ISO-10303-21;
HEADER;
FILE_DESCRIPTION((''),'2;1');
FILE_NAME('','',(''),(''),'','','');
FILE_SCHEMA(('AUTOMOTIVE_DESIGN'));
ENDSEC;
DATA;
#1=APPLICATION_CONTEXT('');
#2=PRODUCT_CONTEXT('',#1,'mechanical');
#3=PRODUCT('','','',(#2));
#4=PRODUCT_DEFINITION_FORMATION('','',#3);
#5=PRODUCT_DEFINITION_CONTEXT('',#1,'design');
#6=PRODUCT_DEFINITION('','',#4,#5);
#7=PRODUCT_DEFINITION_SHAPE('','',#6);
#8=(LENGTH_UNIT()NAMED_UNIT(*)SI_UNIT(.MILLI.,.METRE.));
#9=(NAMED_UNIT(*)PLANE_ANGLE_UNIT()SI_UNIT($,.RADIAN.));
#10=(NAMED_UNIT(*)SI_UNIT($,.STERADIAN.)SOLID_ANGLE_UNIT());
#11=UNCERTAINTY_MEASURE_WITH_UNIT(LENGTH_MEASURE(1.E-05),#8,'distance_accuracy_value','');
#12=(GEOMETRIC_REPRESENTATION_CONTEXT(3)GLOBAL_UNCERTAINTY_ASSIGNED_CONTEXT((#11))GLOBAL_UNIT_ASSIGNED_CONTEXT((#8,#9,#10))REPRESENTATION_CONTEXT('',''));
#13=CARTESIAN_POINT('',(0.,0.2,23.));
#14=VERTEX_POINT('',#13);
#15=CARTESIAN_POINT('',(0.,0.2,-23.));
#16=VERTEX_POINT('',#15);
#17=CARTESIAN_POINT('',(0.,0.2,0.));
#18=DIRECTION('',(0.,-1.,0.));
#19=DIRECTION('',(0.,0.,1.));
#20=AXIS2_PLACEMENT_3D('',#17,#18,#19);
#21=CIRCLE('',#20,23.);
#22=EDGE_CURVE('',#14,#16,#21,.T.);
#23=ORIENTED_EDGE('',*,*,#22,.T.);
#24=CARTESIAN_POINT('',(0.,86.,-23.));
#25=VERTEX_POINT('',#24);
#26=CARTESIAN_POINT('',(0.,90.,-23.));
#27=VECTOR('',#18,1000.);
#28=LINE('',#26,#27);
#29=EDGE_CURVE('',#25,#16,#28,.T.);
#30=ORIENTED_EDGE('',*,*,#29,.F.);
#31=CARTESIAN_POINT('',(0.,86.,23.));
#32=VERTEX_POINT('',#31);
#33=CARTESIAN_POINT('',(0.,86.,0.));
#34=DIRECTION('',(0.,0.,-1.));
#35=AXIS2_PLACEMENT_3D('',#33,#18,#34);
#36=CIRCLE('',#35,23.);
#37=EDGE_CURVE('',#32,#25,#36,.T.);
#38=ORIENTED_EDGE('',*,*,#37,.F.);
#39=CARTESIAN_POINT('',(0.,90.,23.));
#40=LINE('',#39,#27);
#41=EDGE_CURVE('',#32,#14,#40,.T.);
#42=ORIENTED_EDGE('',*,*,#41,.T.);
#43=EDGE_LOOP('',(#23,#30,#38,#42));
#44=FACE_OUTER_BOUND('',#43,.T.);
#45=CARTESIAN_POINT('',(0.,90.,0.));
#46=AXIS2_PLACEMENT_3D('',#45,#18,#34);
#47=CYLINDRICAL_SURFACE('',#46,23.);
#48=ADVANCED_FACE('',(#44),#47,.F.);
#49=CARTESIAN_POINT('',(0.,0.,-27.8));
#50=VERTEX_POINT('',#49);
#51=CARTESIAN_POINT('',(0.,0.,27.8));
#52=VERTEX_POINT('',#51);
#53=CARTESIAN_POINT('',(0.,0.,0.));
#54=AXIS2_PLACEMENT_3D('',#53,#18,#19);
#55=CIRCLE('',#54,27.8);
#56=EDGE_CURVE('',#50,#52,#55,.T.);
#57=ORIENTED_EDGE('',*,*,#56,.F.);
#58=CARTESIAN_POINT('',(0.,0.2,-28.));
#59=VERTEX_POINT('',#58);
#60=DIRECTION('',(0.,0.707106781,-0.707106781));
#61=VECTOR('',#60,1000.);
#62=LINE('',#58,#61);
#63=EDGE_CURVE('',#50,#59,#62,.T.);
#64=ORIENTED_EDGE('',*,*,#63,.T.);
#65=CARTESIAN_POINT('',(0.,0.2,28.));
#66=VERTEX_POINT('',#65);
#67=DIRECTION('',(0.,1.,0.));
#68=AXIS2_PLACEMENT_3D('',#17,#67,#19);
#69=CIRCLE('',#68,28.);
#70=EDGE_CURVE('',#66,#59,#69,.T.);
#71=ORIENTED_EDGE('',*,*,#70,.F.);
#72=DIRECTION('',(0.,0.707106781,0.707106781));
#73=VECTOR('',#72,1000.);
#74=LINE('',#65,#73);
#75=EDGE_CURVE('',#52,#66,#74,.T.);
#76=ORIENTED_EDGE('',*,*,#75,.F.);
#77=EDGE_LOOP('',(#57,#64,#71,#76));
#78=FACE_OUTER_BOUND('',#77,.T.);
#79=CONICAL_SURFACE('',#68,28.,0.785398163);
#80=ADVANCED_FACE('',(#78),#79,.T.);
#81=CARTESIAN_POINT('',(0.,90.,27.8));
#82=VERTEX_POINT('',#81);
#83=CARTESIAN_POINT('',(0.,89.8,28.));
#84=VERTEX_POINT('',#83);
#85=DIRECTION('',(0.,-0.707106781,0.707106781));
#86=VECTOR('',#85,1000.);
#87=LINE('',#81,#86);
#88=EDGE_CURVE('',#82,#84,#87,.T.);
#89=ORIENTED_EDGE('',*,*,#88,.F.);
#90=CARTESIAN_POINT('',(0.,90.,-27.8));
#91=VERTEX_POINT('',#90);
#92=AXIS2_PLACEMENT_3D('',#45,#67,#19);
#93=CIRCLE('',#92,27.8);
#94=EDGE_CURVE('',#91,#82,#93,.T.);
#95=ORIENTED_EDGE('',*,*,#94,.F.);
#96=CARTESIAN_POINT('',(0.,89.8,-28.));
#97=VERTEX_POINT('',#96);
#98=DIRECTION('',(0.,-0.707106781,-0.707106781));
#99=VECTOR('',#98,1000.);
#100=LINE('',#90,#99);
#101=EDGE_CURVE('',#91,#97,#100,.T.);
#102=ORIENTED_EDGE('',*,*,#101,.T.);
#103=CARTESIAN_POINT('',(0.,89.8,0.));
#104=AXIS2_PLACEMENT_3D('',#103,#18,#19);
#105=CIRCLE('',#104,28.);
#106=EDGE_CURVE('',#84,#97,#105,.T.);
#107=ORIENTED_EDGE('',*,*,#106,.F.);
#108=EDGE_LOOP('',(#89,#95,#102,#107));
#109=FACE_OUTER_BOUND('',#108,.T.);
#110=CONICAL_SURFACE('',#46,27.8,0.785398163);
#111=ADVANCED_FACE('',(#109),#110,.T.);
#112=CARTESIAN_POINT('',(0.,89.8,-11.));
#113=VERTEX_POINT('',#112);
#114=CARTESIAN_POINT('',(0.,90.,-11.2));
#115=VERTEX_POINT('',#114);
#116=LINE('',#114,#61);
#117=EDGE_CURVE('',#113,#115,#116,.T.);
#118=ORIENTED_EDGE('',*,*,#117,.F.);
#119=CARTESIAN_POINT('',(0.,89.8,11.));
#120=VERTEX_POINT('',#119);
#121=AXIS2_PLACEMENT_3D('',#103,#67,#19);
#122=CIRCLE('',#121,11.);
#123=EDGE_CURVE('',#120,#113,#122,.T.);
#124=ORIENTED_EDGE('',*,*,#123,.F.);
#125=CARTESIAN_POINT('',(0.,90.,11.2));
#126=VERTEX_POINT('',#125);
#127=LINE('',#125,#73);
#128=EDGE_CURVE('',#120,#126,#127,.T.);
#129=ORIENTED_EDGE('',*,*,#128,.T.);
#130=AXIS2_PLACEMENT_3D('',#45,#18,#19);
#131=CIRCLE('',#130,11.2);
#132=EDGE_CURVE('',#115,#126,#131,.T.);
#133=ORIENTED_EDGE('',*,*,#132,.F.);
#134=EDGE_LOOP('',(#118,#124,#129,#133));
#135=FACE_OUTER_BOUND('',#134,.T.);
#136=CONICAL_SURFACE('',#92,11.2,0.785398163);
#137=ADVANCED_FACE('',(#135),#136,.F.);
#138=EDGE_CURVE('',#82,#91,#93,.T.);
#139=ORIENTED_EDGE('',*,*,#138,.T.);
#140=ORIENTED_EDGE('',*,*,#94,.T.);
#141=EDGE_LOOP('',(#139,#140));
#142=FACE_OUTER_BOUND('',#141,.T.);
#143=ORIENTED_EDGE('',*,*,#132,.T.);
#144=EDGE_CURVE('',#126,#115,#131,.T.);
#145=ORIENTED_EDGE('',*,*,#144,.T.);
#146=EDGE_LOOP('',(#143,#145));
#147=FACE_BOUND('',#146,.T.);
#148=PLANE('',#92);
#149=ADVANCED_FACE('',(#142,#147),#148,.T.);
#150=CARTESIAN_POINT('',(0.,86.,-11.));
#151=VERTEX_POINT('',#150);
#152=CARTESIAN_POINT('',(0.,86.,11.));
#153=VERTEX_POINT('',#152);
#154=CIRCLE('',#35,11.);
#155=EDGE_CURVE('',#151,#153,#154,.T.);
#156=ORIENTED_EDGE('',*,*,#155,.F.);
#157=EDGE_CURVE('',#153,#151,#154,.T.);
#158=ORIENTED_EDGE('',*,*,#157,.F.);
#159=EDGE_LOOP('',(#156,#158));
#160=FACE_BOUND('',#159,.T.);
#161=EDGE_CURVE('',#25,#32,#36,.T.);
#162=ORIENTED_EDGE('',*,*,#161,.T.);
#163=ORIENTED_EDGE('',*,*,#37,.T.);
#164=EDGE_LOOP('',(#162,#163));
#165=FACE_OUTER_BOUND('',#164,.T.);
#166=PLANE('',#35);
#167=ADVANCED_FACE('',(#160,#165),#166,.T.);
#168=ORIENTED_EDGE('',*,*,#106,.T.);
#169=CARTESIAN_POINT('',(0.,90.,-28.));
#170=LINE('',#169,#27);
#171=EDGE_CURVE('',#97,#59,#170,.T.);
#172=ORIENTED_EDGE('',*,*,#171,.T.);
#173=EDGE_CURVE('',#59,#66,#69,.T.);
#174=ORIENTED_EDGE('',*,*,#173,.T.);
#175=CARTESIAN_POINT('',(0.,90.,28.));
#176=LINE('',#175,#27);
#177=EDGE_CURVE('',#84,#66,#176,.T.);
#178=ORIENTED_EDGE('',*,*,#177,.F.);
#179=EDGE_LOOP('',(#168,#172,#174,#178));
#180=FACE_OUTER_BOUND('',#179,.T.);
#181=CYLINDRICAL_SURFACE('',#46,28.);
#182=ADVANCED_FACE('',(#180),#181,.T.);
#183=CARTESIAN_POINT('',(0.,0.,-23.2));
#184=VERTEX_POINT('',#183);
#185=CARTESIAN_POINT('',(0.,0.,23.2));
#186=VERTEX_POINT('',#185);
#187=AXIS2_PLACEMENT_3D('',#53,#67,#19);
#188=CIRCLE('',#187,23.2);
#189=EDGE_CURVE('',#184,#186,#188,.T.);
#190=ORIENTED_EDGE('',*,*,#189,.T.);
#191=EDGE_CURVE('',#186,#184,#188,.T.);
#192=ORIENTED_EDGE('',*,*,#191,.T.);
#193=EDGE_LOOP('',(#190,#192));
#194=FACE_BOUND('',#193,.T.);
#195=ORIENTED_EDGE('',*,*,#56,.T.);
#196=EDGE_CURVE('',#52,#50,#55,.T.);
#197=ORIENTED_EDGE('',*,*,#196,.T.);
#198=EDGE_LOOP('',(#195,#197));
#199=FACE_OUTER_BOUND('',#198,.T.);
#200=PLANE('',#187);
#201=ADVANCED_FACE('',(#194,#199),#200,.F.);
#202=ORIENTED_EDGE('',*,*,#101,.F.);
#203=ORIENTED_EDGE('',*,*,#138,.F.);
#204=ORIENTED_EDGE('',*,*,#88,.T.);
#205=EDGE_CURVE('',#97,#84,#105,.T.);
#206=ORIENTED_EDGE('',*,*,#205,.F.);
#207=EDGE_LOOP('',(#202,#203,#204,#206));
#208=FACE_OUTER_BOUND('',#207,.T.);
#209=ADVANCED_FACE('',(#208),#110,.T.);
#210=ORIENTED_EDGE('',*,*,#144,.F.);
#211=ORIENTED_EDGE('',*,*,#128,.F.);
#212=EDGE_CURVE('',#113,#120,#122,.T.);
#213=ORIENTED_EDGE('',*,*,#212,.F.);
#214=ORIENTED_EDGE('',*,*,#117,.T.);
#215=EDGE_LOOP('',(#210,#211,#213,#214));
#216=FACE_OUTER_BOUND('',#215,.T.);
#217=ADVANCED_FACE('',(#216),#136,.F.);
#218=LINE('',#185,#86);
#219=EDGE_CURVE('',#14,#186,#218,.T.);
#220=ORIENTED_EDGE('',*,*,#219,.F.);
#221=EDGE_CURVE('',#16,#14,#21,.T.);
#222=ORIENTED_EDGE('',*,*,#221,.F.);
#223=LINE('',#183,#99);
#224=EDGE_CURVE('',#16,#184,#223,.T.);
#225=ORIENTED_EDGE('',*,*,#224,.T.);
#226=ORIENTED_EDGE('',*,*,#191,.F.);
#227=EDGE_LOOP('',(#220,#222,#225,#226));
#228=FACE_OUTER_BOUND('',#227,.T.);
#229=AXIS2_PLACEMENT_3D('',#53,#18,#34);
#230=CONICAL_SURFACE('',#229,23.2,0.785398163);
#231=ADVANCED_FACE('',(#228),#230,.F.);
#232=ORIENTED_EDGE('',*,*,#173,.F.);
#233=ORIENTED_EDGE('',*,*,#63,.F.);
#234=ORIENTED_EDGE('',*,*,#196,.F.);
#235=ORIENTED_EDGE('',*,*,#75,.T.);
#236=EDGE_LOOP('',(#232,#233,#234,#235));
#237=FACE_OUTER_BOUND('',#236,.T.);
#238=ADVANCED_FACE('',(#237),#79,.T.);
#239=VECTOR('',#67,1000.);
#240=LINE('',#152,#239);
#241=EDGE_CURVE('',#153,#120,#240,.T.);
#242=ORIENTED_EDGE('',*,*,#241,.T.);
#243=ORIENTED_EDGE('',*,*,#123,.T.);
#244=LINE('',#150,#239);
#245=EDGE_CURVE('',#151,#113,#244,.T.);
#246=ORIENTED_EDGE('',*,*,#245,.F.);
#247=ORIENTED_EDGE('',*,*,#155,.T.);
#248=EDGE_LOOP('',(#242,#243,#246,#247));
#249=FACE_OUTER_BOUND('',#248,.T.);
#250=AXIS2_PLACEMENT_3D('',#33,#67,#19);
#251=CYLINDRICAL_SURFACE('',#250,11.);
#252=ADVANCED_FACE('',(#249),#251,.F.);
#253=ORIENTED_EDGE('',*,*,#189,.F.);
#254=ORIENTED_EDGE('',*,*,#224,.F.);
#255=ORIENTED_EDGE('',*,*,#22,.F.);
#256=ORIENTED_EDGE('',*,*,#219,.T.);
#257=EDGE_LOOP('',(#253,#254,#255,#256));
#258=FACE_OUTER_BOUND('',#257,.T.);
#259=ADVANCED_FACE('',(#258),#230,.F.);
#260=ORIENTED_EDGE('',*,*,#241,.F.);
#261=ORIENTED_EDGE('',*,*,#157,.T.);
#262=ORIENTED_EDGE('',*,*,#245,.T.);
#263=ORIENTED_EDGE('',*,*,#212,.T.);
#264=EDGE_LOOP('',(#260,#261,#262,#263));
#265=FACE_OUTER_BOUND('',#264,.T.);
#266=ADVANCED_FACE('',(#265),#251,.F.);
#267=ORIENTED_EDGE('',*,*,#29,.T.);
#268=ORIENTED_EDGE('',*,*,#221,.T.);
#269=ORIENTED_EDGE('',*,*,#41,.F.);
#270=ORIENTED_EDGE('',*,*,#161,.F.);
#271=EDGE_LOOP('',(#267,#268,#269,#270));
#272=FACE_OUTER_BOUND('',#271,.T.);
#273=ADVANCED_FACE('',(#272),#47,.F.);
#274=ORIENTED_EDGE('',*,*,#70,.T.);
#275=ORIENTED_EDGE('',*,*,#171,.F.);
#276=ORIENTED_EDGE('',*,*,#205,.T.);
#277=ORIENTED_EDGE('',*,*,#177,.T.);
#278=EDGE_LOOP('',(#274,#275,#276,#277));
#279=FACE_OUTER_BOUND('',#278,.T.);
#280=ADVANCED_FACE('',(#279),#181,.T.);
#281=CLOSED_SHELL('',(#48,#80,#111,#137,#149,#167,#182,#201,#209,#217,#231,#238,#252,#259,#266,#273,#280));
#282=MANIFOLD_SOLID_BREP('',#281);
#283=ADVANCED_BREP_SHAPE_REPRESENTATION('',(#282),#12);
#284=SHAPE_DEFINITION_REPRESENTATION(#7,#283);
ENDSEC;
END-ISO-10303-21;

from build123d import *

# Parameters (mm, degrees)
SKETCH_3_R      = 28
SKETCH_3_R_2    = 23
EXTRUDE_1_DEPTH = 90
SKETCH_4_R      = 23.5
SKETCH_4_R_2    = 11
EXTRUDE_2_DEPTH = 4
CHAMFER_1_SIZE  = 0.2


with BuildPart() as part:
    # 草图3 → 凸台-拉伸1 (new body)
    with BuildSketch(Plane(origin=(0, 0, 0), x_dir=(1, 0, 0), z_dir=(0, 1, 0))):
        with Locations(Location((0, 0, 0), (0, 0, 90))):
            Circle(SKETCH_3_R)
        with Locations(Location((0, 0, 0), (0, 0, 90))):
            Circle(SKETCH_3_R_2, mode=Mode.SUBTRACT)
    extrude(amount=EXTRUDE_1_DEPTH)

    # 草图4 → 凸台-拉伸2 (add)
    with BuildSketch(Plane.XZ.offset(-90)):
        Circle(SKETCH_4_R)
        with Locations(Location((0, 0, 0), (0, 0, 270))):
            Circle(SKETCH_4_R_2, mode=Mode.SUBTRACT)
    extrude(amount=EXTRUDE_2_DEPTH)

    # 倒角1
    chamfer_1_edges = [part.edges().sort_by_distance(p)[0] for p in [
        (0, 90, 11),
        (0, 0, 28),
        (0, 90, 28),
        (0, 0, 23),
    ]]
    chamfer(chamfer_1_edges, length=CHAMFER_1_SIZE)


solid = part.part
